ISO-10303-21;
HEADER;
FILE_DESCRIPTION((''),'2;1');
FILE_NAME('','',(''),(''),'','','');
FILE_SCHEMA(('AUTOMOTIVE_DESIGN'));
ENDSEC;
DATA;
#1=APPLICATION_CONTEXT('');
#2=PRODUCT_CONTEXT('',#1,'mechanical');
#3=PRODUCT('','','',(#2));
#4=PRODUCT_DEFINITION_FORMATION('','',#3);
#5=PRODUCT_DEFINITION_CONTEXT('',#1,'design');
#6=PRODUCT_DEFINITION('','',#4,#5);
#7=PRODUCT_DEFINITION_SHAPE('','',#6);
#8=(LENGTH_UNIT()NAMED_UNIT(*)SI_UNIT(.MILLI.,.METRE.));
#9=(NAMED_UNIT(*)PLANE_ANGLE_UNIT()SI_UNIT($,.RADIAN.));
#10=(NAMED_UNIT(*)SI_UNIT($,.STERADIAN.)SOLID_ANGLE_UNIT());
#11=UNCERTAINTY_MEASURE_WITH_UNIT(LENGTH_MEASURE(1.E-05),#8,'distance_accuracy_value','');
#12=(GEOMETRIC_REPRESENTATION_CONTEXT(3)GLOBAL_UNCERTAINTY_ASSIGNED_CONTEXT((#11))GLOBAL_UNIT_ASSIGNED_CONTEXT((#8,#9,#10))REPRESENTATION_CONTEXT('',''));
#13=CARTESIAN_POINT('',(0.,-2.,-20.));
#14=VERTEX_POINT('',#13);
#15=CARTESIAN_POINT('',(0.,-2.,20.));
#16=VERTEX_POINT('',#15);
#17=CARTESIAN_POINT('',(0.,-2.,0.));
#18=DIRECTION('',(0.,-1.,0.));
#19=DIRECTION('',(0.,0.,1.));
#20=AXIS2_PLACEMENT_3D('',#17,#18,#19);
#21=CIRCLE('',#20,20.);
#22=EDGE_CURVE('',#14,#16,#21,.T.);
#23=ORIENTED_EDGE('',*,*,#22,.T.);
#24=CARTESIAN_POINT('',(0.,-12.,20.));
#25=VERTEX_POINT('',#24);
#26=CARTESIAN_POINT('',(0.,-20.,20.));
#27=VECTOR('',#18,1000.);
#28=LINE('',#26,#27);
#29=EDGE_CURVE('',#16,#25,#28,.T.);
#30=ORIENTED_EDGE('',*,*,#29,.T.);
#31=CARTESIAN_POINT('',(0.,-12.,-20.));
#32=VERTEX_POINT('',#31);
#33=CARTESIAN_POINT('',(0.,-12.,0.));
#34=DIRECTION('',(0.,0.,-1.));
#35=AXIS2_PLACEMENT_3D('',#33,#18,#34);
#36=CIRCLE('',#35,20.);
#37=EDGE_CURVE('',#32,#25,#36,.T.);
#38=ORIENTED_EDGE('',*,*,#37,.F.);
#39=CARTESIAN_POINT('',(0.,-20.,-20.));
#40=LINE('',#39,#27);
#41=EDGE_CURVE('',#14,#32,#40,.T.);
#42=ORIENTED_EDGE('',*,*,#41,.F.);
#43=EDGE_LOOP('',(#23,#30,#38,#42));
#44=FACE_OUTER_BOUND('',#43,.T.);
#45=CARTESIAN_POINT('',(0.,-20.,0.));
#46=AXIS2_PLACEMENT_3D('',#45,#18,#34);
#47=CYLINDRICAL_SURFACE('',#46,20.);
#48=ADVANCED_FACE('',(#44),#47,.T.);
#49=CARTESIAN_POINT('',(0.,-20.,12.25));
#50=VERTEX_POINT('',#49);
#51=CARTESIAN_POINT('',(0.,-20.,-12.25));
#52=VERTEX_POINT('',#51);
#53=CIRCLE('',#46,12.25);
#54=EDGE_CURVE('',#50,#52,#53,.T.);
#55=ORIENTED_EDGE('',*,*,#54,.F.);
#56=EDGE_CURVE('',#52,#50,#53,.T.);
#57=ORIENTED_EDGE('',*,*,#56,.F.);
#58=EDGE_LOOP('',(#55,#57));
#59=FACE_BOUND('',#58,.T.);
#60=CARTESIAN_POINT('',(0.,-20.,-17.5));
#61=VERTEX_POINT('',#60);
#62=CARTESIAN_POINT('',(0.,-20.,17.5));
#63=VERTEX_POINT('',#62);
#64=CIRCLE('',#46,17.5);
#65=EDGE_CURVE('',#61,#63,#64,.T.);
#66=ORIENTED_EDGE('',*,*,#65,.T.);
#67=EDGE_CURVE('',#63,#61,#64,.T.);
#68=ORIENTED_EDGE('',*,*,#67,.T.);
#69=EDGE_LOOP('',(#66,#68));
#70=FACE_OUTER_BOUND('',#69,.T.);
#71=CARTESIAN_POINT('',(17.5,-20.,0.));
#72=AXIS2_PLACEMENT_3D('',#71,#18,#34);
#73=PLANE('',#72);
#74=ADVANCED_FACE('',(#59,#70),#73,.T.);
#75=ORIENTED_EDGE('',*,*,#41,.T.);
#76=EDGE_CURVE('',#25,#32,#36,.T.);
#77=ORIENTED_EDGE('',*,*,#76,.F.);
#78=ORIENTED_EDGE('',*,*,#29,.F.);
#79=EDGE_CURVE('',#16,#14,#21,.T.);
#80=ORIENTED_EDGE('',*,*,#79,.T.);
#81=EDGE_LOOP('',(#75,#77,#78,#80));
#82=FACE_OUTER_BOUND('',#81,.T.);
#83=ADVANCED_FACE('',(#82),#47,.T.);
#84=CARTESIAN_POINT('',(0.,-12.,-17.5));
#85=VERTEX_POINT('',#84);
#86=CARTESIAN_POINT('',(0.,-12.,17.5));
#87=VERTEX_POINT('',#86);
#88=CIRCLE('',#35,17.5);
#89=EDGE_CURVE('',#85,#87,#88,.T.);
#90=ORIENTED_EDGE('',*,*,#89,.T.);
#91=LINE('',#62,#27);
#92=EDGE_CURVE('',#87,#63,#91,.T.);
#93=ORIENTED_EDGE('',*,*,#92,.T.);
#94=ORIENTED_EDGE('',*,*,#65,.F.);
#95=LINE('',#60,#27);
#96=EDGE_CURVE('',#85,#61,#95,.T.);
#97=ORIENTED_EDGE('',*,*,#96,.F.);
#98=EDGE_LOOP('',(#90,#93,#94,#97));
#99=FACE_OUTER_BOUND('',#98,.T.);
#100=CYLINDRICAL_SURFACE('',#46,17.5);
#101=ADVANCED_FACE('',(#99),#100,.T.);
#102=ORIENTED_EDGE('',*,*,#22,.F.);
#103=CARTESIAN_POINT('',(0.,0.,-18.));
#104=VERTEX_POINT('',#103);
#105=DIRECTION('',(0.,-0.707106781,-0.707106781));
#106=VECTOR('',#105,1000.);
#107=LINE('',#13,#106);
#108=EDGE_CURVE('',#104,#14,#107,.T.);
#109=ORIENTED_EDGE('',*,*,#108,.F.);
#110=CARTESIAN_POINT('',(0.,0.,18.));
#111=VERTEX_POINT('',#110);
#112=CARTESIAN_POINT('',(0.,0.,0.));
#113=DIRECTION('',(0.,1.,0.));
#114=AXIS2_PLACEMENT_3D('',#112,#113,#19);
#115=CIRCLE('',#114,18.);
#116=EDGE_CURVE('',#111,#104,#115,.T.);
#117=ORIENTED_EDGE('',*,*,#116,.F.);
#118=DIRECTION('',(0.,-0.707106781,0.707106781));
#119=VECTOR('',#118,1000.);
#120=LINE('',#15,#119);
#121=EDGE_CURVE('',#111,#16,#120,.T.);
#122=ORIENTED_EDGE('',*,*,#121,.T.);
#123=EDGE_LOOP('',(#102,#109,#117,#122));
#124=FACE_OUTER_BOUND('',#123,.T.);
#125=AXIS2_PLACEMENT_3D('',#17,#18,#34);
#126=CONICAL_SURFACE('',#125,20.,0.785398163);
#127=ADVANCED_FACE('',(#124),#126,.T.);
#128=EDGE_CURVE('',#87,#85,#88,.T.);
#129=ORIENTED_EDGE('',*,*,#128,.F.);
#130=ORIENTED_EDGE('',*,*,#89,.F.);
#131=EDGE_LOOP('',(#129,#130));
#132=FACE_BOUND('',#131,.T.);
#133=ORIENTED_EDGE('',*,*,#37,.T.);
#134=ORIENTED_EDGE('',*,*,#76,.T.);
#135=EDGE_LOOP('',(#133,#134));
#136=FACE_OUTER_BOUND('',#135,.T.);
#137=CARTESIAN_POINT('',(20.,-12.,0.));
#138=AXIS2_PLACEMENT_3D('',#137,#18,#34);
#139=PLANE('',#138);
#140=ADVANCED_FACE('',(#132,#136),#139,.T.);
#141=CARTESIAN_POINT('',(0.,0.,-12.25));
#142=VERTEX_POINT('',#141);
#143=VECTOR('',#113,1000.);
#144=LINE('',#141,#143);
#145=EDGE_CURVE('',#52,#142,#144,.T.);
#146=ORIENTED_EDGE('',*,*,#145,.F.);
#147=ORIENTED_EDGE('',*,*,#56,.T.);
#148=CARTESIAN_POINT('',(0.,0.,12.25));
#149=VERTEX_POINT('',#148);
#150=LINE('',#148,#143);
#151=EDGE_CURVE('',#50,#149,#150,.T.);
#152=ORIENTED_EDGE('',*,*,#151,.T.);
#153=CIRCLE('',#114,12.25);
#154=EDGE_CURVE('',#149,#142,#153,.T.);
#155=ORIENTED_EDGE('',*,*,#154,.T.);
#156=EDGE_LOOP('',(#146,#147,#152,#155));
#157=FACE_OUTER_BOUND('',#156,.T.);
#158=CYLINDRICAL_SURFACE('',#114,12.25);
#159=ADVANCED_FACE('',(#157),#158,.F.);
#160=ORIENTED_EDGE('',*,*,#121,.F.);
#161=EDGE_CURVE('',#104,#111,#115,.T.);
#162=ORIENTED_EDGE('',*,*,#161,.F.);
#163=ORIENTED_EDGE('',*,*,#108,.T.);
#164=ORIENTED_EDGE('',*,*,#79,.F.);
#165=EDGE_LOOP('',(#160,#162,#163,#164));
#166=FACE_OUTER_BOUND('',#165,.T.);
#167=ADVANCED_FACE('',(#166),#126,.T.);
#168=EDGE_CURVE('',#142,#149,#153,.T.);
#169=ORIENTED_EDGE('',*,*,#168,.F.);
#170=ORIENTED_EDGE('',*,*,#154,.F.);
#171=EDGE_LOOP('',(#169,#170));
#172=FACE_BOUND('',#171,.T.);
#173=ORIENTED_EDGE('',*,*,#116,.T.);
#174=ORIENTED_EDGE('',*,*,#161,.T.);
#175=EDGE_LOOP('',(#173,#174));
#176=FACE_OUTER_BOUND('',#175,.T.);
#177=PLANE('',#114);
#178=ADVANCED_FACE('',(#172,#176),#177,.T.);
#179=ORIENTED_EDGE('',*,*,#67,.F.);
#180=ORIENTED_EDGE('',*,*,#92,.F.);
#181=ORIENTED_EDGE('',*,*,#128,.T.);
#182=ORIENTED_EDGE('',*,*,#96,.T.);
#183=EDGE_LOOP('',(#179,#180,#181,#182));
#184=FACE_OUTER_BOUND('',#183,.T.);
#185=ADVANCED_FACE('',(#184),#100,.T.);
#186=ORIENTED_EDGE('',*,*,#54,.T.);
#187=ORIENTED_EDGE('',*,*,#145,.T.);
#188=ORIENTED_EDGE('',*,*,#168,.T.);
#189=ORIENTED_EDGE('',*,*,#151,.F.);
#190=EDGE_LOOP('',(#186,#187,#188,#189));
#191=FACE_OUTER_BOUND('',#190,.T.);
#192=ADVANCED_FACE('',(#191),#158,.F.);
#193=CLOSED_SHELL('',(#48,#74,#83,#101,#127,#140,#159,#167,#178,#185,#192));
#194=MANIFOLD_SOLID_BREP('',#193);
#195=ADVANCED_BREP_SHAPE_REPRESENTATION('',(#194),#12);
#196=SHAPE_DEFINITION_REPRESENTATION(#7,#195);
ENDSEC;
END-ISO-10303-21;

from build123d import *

# Parameters (mm, degrees)
G3_4_TAPPED_HOLE1_D     = 24.5
G3_4_TAPPED_HOLE1_DEPTH = 58.32
G3_4_TAPPED_HOLE1_TIP   = 7.360542583
CHAMFER1_SIZE           = 2


with BuildPart() as part:
    # Sketch1 → Revolve1 (revolve)
    with BuildSketch(Plane.XY, mode=Mode.PRIVATE) as revolve1_sk:
        Polygon((0, 0), (20, 0), (20, -12), (17.5, -12), (17.5, -20), (0, -20), align=None)
    revolve(revolve1_sk.sketch.rotate(Axis((0, -20, 0), (0, 1, 0)), 90), axis=Axis((0, -20, 0), (0, 1, 0)))

    # G3/4 Tapped Hole1
    with Locations(Plane(origin=(0, 0, 0), x_dir=(1, 0, 0), z_dir=(0, 1, 0))):
        with Locations((0, 0)):
            Hole(G3_4_TAPPED_HOLE1_D / 2, depth=G3_4_TAPPED_HOLE1_DEPTH)
            with Locations((0, 0, -(G3_4_TAPPED_HOLE1_DEPTH + G3_4_TAPPED_HOLE1_TIP / 2))):  # 118° drill point
                Cone(0, G3_4_TAPPED_HOLE1_D / 2, G3_4_TAPPED_HOLE1_TIP, mode=Mode.SUBTRACT)

    # Chamfer1
    chamfer1_edges = [part.edges().sort_by_distance(p)[0] for p in [
        (0, 0, 20),
    ]]
    chamfer(chamfer1_edges, length=CHAMFER1_SIZE)


solid = part.part
